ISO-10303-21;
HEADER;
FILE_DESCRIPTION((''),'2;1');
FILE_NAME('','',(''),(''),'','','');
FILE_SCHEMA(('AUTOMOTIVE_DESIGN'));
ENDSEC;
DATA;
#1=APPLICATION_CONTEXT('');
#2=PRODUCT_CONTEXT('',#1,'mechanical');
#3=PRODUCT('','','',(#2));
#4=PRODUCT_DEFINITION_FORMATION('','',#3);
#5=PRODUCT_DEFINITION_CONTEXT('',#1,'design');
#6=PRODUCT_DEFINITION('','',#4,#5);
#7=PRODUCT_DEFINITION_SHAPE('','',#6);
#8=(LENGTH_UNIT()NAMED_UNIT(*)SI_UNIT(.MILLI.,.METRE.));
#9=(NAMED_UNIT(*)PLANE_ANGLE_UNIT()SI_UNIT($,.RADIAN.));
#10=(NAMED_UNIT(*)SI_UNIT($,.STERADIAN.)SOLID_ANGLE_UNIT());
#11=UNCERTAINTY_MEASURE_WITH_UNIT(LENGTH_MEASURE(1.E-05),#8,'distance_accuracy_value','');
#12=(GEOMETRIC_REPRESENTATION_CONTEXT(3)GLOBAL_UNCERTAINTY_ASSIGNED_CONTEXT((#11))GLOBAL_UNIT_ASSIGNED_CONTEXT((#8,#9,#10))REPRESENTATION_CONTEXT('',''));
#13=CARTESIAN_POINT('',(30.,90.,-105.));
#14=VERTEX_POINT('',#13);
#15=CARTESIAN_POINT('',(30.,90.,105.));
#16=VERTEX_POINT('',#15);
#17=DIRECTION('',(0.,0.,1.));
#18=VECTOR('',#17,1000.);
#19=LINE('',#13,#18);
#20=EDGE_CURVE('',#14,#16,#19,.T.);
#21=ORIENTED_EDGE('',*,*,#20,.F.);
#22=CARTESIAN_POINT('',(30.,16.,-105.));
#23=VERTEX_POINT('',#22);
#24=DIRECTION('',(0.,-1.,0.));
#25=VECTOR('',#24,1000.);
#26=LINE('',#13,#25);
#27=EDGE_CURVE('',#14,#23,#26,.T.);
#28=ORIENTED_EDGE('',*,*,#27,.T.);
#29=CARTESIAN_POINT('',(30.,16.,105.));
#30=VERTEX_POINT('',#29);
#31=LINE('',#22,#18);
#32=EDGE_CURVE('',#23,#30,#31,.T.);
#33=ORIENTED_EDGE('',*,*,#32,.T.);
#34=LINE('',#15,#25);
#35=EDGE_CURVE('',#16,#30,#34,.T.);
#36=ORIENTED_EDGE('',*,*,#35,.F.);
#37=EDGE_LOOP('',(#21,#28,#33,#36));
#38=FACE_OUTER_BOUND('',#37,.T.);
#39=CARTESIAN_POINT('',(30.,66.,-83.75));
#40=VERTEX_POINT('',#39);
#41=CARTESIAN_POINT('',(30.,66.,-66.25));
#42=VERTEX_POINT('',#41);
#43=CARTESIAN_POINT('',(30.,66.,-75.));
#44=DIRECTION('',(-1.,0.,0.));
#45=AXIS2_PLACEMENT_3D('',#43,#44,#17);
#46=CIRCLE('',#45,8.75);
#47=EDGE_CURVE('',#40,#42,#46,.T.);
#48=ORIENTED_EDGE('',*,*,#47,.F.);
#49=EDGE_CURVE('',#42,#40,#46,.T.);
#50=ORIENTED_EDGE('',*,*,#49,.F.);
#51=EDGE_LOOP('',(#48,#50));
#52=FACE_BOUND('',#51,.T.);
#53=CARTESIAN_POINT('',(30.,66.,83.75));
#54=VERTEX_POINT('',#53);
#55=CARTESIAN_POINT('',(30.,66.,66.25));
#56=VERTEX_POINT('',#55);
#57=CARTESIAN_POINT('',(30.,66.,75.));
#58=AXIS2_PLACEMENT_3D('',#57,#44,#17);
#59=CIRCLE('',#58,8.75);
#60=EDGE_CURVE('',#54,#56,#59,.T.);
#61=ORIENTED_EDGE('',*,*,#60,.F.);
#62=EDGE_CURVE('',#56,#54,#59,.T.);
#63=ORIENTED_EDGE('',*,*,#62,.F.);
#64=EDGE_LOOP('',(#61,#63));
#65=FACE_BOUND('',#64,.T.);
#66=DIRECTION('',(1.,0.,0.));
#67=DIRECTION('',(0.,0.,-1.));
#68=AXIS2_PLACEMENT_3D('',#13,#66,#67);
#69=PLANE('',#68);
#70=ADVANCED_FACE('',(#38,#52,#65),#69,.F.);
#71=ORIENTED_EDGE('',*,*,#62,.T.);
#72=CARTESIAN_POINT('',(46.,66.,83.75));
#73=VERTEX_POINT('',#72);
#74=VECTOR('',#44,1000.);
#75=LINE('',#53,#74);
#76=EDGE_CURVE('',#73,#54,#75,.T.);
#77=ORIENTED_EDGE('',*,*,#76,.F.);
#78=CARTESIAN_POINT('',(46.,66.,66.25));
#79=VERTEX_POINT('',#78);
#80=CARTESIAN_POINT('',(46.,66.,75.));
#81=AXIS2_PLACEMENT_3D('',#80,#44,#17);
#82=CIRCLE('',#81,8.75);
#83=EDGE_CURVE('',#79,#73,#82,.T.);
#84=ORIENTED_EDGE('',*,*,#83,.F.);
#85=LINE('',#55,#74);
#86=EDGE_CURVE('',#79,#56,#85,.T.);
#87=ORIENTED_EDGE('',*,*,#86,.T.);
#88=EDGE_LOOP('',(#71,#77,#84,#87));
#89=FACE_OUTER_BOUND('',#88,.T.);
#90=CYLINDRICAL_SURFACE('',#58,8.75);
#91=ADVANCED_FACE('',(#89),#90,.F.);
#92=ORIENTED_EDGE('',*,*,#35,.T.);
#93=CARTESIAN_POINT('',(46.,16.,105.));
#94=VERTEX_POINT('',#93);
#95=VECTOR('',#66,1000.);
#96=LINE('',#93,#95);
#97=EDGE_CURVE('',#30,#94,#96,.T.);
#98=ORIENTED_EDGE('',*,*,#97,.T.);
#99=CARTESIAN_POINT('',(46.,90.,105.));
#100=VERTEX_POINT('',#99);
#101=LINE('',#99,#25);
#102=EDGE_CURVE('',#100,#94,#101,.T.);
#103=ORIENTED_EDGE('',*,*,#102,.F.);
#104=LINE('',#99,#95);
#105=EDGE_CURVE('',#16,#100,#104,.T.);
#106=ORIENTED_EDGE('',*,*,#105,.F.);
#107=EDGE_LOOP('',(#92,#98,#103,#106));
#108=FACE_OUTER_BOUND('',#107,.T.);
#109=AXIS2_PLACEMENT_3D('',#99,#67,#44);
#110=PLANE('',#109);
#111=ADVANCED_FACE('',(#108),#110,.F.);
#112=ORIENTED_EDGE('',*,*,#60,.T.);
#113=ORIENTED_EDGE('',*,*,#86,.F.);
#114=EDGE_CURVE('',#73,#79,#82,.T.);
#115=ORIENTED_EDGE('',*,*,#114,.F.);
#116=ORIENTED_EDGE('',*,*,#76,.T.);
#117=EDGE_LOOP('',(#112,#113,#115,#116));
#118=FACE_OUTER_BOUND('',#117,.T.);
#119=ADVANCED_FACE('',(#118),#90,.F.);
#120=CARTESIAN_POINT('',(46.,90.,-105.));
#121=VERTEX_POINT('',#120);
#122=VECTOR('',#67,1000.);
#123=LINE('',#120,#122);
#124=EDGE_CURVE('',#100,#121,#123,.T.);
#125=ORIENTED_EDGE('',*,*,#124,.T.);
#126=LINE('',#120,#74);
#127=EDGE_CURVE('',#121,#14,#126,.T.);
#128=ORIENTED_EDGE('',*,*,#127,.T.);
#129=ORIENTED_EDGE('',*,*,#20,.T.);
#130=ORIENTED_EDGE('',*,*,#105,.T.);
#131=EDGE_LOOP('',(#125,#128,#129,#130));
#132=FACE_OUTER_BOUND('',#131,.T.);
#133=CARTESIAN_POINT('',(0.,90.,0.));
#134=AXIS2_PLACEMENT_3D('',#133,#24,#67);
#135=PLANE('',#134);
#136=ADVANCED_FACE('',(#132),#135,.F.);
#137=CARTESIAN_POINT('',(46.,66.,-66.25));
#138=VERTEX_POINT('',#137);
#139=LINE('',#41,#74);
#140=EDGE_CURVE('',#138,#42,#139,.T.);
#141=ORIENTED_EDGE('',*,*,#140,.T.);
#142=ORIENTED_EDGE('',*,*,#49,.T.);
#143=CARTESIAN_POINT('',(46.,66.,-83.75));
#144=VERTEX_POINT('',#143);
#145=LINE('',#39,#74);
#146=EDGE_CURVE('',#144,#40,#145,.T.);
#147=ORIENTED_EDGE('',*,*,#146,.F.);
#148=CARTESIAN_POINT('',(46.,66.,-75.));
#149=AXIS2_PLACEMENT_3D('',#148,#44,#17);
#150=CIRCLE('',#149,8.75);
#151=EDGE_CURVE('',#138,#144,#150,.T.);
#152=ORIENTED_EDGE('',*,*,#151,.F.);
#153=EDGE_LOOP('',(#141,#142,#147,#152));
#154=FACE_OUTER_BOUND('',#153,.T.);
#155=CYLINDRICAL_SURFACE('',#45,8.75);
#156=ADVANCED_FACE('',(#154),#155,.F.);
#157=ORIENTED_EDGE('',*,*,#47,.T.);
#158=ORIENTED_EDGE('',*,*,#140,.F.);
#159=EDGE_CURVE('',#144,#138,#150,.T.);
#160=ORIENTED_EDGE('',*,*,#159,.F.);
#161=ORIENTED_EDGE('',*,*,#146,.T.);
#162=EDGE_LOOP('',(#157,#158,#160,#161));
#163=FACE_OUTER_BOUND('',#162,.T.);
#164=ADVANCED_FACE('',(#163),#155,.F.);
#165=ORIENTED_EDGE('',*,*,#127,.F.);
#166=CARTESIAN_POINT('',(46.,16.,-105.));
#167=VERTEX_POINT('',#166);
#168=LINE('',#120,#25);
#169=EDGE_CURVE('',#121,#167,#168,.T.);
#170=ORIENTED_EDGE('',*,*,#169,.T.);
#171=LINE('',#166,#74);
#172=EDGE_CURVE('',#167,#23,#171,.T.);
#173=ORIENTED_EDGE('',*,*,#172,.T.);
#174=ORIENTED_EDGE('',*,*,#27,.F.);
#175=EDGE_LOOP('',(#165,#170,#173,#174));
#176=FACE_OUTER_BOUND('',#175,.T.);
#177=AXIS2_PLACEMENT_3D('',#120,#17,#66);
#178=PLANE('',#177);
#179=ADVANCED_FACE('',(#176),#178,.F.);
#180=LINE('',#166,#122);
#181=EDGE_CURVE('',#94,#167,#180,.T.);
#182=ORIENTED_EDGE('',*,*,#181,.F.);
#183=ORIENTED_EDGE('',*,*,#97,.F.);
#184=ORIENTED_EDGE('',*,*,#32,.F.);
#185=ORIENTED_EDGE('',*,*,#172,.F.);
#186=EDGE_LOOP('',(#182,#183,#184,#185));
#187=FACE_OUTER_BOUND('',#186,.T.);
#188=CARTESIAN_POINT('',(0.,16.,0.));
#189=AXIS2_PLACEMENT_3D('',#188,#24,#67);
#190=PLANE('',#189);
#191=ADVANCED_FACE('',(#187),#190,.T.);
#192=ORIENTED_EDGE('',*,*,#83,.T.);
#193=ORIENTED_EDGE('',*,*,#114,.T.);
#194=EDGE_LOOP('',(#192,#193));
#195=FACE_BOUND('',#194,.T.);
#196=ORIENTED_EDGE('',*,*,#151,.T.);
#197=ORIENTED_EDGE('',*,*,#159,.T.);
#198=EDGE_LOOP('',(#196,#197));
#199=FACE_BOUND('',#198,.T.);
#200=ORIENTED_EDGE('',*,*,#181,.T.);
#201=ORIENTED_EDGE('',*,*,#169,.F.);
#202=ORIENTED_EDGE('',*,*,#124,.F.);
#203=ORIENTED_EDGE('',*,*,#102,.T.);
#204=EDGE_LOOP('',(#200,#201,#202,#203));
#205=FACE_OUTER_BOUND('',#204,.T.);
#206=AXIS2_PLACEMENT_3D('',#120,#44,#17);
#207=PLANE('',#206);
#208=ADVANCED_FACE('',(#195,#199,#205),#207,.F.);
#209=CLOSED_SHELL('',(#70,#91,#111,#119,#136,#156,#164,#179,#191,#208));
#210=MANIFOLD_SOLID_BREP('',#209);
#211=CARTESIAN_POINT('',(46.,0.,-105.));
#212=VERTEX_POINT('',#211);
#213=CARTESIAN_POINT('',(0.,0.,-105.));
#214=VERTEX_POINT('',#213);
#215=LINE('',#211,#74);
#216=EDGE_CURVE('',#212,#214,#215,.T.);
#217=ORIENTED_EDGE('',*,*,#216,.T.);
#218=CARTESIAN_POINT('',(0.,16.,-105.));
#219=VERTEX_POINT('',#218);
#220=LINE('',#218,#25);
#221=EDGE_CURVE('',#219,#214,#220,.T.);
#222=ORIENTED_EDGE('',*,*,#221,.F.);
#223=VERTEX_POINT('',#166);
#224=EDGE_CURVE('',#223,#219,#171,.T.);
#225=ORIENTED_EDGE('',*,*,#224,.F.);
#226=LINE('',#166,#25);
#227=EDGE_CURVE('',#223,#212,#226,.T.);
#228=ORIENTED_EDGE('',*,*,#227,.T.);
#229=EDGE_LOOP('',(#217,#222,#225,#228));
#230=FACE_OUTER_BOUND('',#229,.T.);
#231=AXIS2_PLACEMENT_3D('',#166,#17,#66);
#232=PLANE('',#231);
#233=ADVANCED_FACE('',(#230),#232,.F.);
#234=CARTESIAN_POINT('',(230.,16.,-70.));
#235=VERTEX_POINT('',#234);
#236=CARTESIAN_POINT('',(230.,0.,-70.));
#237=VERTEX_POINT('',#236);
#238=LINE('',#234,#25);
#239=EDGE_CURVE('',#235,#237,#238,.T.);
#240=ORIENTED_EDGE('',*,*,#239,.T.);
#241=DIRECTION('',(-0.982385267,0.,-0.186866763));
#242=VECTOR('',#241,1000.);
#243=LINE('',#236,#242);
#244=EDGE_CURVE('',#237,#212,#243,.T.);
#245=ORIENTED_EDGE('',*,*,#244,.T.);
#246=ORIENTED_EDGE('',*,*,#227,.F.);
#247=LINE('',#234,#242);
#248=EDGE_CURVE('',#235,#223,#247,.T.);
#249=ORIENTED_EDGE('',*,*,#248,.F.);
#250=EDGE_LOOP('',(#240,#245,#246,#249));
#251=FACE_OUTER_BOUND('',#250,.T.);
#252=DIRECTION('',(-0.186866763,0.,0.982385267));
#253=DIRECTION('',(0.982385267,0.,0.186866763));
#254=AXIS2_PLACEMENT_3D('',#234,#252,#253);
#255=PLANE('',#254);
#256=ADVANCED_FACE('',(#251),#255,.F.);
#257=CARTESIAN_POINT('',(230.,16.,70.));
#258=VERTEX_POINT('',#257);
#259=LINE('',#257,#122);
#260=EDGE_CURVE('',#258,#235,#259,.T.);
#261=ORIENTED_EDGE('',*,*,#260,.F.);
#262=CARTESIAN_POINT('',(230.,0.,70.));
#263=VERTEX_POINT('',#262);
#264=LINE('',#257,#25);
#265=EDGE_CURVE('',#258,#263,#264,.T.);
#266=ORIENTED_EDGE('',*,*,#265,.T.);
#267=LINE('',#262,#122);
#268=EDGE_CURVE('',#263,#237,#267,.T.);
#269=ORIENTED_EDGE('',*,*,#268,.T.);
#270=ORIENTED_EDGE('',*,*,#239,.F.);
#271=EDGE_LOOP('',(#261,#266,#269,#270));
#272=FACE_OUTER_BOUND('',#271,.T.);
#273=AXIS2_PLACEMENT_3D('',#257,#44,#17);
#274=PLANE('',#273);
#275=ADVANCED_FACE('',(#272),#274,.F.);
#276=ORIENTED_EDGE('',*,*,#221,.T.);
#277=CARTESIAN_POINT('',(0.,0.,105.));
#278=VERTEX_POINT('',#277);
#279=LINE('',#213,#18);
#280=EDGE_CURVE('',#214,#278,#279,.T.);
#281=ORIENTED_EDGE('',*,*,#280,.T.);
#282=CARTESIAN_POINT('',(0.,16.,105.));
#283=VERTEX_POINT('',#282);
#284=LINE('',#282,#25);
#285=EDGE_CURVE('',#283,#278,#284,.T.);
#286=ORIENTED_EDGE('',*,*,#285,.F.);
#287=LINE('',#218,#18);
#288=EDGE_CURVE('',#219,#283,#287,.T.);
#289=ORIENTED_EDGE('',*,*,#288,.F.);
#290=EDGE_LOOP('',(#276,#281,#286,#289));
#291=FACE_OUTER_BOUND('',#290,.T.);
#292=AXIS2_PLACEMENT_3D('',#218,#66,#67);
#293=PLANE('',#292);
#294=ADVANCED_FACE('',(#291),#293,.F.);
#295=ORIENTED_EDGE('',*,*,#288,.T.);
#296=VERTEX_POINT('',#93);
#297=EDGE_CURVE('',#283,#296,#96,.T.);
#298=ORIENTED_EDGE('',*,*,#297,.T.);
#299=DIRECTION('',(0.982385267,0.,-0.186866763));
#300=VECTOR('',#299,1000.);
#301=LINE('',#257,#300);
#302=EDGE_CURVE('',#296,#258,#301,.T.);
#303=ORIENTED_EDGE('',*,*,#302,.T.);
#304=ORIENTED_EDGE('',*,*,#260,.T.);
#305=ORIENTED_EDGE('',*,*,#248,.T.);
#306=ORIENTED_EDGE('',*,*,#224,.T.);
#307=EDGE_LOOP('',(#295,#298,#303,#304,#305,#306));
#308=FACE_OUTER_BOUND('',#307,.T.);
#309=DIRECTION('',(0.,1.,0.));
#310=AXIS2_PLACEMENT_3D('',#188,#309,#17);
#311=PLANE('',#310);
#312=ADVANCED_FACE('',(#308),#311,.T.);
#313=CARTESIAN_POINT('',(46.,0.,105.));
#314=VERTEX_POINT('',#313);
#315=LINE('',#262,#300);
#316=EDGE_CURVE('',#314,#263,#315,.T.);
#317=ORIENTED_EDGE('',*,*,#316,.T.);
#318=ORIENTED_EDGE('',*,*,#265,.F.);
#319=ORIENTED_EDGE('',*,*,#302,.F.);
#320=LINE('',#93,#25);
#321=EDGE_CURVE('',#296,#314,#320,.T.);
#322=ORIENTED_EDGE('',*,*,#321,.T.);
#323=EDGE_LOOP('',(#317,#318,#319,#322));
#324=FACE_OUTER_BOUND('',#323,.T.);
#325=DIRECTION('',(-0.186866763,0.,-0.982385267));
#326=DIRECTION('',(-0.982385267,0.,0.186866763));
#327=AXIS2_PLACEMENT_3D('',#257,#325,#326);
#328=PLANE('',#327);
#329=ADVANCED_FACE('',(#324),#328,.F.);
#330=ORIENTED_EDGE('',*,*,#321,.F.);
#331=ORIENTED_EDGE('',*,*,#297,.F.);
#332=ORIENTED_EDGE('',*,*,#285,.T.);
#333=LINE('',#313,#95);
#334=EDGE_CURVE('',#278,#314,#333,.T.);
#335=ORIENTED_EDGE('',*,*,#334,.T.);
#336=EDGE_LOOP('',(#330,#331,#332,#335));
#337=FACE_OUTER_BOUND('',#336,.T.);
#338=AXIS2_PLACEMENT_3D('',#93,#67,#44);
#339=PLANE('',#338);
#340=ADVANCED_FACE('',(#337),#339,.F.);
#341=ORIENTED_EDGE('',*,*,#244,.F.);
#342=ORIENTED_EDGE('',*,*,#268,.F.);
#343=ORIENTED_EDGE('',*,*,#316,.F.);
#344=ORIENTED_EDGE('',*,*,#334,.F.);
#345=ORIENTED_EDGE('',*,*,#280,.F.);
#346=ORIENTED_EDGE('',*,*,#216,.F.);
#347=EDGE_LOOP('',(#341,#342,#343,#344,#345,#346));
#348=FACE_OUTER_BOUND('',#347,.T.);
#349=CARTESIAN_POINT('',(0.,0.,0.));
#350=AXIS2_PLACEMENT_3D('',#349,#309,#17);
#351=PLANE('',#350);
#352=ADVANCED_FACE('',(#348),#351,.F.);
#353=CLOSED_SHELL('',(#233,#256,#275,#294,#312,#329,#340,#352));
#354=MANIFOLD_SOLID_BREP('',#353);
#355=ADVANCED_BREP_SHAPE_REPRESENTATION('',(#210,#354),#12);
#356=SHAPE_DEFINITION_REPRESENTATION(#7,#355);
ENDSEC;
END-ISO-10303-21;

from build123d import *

# Parameters (mm, degrees)
EXTRUDE_1_DEPTH              = 16
SKETCH_2_W                   = 16
SKETCH_2_H                   = 210
EXTRUDE_2_DEPTH              = 74
HOLE_WIZARD_M20_1_AT_2_COUNT = 2
HOLE_WIZARD_M20_1_AT_2_PITCH = 150


with BuildPart() as part:
    # 草图1 → 凸台-拉伸1 (new body)
    with BuildSketch(Plane(origin=(0, 0, 0), x_dir=(1, 0, 0), z_dir=(0, 1, 0))):
        Polygon((230, -70), (230, 70), (46, 105), (0, 105), (0, -105), (46, -105), align=None)
    extrude(amount=EXTRUDE_1_DEPTH)


with BuildPart() as body_2:
    # 草图2 → 凸台-拉伸2 (new body)
    with BuildSketch(Plane(origin=(0, 16, 0), x_dir=(1, 0, 0), z_dir=(0, 1, 0))):
        with Locations((38, 0)):
            Rectangle(SKETCH_2_W, SKETCH_2_H)
    extrude(amount=EXTRUDE_2_DEPTH)

    # 草图4 → M20 螺纹孔1 (revolve, cut)
    with BuildSketch(Plane(origin=(30, 66, -75), x_dir=(0, 0, 1), z_dir=(0, 1, 0))):
        Polygon((0, 0), (0, 57.757530416), (8.75, 52.5), (8.75, 0), align=None)
    hole_wizard_m20_1 = revolve(axis=Axis((23.65, 66, -75), (1, 0, 0)), mode=Mode.SUBTRACT)

    # M20 螺纹孔1 at 2: M20 螺纹孔1 ×2
    with Locations(*[(0, 0, i * HOLE_WIZARD_M20_1_AT_2_PITCH) for i in range(1, HOLE_WIZARD_M20_1_AT_2_COUNT)]):
        add(hole_wizard_m20_1, mode=Mode.SUBTRACT)


solid = Compound([part.part, body_2.part])
